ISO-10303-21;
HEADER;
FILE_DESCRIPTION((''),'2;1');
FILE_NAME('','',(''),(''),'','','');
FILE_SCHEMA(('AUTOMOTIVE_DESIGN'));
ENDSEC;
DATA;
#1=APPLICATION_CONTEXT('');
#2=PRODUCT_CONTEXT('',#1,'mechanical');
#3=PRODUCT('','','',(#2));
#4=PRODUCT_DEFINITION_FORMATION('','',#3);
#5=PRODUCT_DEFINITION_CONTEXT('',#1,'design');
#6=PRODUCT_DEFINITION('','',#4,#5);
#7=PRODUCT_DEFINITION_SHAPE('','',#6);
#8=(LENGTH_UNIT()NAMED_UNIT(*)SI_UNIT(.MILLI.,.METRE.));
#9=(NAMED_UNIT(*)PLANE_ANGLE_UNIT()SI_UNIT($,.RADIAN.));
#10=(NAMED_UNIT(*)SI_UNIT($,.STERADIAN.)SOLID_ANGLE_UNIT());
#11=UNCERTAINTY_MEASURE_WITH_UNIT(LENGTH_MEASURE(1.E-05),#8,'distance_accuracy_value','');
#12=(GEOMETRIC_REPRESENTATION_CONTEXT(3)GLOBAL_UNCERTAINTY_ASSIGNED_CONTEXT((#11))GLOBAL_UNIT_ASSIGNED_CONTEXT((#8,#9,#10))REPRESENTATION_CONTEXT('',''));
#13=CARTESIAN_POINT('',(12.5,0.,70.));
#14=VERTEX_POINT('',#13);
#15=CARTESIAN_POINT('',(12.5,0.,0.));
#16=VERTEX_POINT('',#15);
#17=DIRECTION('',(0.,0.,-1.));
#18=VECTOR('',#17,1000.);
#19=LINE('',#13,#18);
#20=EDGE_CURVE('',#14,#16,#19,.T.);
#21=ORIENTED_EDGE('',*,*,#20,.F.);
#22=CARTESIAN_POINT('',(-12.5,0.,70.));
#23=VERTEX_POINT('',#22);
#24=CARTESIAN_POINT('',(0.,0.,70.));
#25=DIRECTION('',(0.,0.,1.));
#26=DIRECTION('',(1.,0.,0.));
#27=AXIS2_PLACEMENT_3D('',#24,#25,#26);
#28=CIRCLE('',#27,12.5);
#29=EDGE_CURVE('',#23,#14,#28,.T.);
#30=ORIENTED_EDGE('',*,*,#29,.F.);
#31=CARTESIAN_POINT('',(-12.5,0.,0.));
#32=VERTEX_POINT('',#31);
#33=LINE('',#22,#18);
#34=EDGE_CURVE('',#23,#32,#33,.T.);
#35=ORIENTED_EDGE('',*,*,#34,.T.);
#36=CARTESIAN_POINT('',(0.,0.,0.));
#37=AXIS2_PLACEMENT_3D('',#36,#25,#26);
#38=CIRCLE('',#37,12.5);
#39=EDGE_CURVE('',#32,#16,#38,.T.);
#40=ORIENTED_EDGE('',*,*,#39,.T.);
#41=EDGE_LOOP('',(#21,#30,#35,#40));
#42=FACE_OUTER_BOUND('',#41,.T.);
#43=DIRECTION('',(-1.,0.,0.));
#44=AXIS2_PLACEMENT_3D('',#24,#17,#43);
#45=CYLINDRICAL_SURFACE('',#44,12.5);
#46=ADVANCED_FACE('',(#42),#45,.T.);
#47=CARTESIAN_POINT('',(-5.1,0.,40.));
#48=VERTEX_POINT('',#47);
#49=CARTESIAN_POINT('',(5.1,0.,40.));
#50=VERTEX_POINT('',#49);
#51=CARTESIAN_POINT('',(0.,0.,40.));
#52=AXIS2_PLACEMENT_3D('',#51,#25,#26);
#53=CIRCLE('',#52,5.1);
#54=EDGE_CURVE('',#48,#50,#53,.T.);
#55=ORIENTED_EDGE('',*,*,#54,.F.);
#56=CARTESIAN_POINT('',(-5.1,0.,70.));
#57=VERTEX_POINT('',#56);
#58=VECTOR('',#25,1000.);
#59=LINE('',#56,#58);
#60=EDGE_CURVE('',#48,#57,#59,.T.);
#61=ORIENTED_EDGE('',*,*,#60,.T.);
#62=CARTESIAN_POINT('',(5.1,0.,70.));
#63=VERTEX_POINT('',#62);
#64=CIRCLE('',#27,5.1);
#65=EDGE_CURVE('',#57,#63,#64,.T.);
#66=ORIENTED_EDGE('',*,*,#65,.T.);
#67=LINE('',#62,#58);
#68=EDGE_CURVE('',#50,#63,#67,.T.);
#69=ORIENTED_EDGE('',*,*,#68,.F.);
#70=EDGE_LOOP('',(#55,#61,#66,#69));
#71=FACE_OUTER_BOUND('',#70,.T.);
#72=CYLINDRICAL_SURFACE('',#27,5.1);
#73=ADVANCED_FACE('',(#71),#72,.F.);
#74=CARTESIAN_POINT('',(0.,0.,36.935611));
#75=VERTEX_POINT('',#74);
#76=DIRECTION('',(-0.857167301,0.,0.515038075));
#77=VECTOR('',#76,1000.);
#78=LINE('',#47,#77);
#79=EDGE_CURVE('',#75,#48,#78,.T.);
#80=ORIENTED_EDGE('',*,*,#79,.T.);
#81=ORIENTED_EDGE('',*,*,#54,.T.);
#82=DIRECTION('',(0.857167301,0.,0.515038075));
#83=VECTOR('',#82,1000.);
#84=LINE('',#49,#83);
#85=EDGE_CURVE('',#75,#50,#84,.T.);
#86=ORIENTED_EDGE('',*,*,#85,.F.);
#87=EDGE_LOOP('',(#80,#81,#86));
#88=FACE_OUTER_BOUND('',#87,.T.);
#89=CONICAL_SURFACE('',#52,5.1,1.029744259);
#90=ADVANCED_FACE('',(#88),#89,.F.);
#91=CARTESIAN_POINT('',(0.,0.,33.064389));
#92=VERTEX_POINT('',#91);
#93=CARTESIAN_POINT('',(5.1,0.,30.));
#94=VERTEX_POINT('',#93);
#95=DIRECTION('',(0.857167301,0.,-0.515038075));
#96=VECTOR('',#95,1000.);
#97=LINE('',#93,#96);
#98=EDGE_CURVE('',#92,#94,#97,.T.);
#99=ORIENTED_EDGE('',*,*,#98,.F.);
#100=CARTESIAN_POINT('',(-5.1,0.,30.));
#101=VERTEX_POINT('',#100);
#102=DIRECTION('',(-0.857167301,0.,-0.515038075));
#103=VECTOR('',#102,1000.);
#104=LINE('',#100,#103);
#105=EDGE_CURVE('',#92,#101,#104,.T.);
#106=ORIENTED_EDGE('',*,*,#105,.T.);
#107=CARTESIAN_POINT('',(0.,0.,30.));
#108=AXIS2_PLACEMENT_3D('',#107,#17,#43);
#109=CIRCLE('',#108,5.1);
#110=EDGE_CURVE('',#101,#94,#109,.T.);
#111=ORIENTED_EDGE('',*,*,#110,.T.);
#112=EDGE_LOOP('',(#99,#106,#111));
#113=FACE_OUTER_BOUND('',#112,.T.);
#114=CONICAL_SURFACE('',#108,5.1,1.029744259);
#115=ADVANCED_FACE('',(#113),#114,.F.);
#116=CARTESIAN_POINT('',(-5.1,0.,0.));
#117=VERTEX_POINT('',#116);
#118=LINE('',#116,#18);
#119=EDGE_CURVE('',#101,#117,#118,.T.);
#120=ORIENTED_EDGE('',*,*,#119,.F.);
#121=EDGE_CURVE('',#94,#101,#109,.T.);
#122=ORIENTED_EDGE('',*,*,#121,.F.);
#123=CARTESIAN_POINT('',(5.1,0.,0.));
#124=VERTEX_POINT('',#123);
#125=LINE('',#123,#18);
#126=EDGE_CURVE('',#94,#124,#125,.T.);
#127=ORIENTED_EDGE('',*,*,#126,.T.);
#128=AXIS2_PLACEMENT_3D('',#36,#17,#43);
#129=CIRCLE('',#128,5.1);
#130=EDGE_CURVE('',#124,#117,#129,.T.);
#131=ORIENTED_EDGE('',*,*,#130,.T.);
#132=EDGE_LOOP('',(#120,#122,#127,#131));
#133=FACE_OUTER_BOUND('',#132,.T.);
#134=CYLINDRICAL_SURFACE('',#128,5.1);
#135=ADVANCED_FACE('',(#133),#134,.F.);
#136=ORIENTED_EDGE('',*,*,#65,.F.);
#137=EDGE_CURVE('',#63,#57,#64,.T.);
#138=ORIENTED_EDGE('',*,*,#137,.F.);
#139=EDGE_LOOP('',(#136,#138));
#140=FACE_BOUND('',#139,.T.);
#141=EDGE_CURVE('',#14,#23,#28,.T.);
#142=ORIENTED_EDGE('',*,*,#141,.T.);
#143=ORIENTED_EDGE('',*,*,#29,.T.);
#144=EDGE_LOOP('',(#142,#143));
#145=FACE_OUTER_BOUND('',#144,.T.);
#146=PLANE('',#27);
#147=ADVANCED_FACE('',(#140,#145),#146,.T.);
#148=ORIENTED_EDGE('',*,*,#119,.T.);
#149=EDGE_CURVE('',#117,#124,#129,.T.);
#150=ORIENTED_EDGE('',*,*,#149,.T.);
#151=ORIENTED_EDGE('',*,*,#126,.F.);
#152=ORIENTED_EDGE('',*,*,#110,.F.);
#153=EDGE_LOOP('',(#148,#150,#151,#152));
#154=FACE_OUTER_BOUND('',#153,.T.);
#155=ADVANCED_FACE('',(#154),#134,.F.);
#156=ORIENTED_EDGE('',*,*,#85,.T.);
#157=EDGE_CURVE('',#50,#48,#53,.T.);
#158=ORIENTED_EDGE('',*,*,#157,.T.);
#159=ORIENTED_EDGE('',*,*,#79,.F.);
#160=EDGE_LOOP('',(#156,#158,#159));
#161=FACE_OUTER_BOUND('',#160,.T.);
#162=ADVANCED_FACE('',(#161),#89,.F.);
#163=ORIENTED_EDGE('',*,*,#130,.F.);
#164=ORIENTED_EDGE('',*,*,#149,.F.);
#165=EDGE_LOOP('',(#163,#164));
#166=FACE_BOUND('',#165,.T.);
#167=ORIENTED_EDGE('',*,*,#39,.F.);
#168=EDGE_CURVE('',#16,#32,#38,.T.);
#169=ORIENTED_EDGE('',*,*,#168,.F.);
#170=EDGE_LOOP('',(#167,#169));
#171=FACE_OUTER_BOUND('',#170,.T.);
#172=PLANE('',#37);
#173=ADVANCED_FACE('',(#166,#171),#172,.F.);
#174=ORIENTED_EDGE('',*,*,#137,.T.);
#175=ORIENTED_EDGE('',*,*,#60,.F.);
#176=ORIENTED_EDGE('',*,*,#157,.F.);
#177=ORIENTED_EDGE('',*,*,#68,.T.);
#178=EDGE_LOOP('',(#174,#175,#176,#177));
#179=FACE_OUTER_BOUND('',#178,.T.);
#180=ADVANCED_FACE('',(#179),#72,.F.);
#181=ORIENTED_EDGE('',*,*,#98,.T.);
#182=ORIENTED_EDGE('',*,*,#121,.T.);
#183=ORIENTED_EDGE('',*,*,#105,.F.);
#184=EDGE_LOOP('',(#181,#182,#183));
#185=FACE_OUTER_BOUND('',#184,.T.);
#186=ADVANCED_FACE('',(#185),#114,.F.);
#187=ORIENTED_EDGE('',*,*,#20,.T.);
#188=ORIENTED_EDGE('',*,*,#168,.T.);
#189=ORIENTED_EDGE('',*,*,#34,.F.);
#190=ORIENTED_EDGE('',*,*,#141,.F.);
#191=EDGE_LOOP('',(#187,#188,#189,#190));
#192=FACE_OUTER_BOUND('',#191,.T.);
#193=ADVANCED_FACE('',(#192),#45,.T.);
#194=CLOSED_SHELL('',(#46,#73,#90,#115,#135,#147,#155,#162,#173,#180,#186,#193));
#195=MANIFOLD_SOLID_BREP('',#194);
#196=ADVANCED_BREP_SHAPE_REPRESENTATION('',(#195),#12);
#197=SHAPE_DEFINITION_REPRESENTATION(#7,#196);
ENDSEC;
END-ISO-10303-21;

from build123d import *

# Parameters (mm, degrees)
SKETCH1_R              = 12.5
BOSS_EXTRUDE1_DEPTH    = 70
M12_TAPPED_HOLE1_D     = 10.2
M12_TAPPED_HOLE1_DEPTH = 30
M12_TAPPED_HOLE1_TIP   = 3.064389157
M12_TAPPED_HOLE2_D     = 10.2
M12_TAPPED_HOLE2_DEPTH = 30
M12_TAPPED_HOLE2_TIP   = 3.064389157


with BuildPart() as part:
    # Sketch1 → Boss-Extrude1 (new body)
    with BuildSketch(Plane.XY):
        Circle(SKETCH1_R)
    extrude(amount=BOSS_EXTRUDE1_DEPTH)

    # M12 Tapped Hole1
    with Locations(Plane.XY.offset(70)):
        with Locations((0, 0)):
            Hole(M12_TAPPED_HOLE1_D / 2, depth=M12_TAPPED_HOLE1_DEPTH)
            with Locations((0, 0, -(M12_TAPPED_HOLE1_DEPTH + M12_TAPPED_HOLE1_TIP / 2))):  # 118° drill point
                Cone(0, M12_TAPPED_HOLE1_D / 2, M12_TAPPED_HOLE1_TIP, mode=Mode.SUBTRACT)

    # M12 Tapped Hole2
    with Locations(Plane(origin=(0, 0, 0), x_dir=(-1, 0, 0), z_dir=(0, 0, -1))):
        with Locations((0, 0)):
            Hole(M12_TAPPED_HOLE2_D / 2, depth=M12_TAPPED_HOLE2_DEPTH)
            with Locations((0, 0, -(M12_TAPPED_HOLE2_DEPTH + M12_TAPPED_HOLE2_TIP / 2))):  # 118° drill point
                Cone(0, M12_TAPPED_HOLE2_D / 2, M12_TAPPED_HOLE2_TIP, mode=Mode.SUBTRACT)


solid = part.part
